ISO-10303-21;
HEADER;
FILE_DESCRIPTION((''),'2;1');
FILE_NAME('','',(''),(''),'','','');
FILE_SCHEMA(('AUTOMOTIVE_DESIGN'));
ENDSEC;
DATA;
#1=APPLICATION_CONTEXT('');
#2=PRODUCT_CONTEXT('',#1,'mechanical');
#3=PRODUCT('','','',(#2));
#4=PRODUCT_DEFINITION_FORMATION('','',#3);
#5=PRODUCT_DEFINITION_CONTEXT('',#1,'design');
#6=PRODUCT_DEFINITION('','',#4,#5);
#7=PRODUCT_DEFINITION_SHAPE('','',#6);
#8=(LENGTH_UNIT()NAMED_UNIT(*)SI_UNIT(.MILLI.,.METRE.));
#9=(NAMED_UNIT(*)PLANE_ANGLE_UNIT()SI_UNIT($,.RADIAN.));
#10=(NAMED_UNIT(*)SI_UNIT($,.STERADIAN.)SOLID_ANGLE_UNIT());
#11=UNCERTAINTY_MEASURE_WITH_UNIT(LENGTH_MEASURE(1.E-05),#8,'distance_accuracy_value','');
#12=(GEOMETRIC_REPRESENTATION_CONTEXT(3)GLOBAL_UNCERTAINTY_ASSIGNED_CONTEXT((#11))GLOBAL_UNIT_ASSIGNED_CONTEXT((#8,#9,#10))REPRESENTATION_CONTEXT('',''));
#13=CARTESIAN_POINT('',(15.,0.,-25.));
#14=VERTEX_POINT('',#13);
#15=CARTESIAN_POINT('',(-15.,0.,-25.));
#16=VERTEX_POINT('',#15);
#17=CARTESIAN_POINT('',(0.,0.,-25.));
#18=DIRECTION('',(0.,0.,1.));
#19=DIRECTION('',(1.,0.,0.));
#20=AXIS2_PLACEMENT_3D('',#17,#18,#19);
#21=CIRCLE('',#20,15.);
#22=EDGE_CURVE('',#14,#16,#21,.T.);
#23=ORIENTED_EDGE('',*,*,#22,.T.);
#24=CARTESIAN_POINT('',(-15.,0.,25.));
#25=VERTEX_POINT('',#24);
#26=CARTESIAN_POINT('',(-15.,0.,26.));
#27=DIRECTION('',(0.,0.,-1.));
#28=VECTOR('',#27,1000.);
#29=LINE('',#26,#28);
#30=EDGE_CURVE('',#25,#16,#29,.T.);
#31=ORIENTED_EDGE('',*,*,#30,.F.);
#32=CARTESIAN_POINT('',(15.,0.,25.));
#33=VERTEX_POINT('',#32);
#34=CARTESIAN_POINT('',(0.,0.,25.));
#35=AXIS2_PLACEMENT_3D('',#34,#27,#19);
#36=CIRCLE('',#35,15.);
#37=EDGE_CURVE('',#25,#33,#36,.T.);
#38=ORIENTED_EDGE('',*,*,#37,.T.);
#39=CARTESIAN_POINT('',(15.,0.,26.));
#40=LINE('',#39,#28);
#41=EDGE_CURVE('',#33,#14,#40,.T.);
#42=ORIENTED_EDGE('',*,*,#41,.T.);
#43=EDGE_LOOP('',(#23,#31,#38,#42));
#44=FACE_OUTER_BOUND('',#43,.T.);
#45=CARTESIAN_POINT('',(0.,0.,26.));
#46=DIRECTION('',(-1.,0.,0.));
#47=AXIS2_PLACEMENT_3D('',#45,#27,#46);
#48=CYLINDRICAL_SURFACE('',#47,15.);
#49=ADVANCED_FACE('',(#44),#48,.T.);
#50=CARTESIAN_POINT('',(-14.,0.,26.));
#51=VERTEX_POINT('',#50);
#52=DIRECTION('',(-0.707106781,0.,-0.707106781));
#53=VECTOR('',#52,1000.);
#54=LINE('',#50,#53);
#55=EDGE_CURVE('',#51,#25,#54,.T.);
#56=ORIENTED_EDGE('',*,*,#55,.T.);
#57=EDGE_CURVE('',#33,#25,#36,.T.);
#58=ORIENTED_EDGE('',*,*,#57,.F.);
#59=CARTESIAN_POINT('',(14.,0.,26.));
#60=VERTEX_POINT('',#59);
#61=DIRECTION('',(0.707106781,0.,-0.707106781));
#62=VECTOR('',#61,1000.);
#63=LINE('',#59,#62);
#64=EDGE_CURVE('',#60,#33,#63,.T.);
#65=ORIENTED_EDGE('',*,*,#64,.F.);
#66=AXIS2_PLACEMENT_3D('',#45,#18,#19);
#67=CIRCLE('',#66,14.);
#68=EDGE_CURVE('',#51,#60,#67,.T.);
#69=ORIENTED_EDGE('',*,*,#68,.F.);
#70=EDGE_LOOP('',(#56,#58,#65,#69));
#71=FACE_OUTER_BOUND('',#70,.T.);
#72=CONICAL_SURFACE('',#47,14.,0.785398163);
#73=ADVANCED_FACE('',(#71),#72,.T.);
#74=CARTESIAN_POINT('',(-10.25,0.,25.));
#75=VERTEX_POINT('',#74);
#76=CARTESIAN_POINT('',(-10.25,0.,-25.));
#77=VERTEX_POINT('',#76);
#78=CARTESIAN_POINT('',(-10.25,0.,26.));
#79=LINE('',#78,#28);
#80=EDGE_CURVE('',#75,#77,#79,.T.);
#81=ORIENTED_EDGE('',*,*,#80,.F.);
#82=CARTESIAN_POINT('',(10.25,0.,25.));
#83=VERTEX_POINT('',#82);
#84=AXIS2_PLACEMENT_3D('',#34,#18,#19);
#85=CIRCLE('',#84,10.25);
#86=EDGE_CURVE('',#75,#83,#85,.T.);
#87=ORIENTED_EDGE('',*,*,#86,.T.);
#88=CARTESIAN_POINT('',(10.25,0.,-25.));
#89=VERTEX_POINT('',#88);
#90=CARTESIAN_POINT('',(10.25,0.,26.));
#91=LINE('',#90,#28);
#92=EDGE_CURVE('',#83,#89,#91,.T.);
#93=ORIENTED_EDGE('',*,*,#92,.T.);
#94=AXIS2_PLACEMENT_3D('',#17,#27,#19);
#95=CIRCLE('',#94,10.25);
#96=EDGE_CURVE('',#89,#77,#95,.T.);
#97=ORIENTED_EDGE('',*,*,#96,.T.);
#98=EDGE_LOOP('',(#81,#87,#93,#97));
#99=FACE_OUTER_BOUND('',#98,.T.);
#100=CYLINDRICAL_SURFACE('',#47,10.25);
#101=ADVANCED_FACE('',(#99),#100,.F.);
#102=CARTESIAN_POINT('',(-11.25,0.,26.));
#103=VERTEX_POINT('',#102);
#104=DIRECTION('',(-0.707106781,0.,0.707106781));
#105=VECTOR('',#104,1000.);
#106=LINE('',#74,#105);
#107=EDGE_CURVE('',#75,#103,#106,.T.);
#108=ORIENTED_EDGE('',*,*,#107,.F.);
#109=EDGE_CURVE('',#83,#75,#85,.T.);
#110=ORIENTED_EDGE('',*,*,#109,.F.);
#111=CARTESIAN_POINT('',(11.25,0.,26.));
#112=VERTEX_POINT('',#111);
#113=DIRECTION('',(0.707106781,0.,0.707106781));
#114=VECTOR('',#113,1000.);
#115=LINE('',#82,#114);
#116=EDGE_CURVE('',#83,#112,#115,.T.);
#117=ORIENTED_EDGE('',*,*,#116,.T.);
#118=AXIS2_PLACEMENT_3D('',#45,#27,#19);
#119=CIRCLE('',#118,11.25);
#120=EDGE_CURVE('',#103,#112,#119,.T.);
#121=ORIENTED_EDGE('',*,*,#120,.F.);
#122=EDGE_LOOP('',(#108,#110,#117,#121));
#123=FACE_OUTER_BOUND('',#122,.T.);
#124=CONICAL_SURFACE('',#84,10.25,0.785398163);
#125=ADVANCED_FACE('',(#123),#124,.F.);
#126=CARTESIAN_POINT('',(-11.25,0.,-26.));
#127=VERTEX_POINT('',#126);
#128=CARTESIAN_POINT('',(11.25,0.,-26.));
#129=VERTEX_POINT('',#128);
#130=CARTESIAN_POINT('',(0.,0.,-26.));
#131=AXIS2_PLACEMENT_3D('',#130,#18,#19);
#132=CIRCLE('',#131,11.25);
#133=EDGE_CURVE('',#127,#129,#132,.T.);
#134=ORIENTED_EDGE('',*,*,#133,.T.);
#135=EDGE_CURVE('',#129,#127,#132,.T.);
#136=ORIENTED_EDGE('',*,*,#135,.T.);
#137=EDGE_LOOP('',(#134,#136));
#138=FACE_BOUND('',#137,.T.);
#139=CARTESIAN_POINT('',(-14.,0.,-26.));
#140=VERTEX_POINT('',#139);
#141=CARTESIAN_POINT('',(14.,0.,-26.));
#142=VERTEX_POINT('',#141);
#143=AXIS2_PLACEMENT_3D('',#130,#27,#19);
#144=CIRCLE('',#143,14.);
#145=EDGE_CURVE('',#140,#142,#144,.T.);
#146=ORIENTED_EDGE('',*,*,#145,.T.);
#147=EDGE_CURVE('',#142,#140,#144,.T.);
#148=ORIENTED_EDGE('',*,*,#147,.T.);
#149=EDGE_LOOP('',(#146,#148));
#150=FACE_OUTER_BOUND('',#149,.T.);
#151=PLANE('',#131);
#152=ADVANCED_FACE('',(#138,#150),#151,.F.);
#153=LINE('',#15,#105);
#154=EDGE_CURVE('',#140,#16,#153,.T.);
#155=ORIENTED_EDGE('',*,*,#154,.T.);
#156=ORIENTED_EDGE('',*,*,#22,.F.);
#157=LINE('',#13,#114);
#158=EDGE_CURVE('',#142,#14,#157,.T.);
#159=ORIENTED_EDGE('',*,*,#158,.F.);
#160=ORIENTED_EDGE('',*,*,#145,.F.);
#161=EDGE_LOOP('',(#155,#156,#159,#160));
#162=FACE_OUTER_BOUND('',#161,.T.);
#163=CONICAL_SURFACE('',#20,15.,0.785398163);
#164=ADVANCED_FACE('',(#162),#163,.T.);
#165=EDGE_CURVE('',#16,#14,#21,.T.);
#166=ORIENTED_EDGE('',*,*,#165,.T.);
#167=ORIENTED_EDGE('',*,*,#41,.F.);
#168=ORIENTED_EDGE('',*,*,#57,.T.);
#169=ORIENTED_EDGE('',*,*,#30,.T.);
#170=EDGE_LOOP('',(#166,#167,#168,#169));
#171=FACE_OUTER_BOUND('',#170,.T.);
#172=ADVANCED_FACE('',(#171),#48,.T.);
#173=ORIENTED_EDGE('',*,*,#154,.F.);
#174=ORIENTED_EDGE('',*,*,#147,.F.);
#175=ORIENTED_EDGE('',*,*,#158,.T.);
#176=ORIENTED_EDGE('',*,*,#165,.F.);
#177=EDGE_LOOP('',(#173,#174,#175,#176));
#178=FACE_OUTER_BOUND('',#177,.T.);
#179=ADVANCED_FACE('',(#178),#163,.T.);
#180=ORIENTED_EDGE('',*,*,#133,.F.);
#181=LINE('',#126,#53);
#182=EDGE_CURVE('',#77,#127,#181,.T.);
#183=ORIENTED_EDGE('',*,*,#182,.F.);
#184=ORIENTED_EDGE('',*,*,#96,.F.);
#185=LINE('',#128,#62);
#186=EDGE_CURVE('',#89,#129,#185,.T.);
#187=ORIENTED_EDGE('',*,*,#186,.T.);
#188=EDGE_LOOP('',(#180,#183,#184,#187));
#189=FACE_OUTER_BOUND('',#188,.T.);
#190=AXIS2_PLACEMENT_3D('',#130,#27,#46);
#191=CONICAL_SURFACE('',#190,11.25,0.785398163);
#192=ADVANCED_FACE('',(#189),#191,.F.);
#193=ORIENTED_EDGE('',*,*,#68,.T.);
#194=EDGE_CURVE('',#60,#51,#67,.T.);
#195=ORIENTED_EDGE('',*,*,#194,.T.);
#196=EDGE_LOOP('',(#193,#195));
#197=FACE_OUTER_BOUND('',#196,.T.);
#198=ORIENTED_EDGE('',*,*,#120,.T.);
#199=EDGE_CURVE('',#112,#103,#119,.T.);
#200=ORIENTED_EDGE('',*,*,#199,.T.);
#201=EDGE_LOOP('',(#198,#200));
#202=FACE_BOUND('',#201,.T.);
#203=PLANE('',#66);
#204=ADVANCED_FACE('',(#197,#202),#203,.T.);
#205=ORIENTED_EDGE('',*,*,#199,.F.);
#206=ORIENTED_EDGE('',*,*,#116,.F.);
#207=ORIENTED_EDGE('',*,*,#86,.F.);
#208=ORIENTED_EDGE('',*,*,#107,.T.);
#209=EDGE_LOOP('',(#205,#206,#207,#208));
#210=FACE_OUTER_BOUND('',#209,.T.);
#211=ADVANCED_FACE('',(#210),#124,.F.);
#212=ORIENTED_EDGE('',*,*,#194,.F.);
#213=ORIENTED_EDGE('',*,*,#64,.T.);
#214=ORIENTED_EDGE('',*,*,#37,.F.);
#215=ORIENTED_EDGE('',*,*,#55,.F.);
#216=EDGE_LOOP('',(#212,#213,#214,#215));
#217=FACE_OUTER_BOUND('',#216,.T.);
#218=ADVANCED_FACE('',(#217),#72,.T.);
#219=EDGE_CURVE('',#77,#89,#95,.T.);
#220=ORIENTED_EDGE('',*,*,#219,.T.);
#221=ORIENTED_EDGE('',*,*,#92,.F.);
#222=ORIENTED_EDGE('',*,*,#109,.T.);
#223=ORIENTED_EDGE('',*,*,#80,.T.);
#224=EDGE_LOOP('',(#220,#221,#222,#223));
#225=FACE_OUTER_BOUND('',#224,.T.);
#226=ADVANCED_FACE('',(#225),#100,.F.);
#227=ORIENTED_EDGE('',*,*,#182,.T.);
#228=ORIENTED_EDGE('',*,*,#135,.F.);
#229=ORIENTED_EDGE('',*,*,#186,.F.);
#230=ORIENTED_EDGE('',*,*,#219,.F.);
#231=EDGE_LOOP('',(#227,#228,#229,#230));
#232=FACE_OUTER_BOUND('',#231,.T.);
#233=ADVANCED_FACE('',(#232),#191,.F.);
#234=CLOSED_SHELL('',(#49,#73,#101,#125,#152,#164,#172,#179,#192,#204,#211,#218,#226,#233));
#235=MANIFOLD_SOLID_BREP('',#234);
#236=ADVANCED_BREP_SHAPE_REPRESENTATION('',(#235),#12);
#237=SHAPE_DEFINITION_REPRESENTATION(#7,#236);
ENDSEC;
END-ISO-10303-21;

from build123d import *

# Parameters (mm, degrees)
SKETCH_1_R      = 15
SKETCH_1_R_2    = 10.25
EXTRUDE_1_DEPTH = 26
CHAMFER_1_SIZE  = 1


with BuildPart() as part:
    # 草图1 → 凸台-拉伸1 (new, symmetric)
    with BuildSketch(Plane.XY):
        with Locations(Location((0, 0, 0), (0, 0, 180))):
            Circle(SKETCH_1_R)
        with Locations(Location((0, 0, 0), (0, 0, 180))):
            Circle(SKETCH_1_R_2, mode=Mode.SUBTRACT)
    extrude(amount=EXTRUDE_1_DEPTH, both=True)

    # 倒角1
    chamfer_1_edges = [part.edges().sort_by_distance(p)[0] for p in [
        (15, 0, -26),
        (15, 0, 26),
        (10.25, 0, -26),
        (10.25, 0, 26),
    ]]
    chamfer(chamfer_1_edges, length=CHAMFER_1_SIZE)


solid = part.part
